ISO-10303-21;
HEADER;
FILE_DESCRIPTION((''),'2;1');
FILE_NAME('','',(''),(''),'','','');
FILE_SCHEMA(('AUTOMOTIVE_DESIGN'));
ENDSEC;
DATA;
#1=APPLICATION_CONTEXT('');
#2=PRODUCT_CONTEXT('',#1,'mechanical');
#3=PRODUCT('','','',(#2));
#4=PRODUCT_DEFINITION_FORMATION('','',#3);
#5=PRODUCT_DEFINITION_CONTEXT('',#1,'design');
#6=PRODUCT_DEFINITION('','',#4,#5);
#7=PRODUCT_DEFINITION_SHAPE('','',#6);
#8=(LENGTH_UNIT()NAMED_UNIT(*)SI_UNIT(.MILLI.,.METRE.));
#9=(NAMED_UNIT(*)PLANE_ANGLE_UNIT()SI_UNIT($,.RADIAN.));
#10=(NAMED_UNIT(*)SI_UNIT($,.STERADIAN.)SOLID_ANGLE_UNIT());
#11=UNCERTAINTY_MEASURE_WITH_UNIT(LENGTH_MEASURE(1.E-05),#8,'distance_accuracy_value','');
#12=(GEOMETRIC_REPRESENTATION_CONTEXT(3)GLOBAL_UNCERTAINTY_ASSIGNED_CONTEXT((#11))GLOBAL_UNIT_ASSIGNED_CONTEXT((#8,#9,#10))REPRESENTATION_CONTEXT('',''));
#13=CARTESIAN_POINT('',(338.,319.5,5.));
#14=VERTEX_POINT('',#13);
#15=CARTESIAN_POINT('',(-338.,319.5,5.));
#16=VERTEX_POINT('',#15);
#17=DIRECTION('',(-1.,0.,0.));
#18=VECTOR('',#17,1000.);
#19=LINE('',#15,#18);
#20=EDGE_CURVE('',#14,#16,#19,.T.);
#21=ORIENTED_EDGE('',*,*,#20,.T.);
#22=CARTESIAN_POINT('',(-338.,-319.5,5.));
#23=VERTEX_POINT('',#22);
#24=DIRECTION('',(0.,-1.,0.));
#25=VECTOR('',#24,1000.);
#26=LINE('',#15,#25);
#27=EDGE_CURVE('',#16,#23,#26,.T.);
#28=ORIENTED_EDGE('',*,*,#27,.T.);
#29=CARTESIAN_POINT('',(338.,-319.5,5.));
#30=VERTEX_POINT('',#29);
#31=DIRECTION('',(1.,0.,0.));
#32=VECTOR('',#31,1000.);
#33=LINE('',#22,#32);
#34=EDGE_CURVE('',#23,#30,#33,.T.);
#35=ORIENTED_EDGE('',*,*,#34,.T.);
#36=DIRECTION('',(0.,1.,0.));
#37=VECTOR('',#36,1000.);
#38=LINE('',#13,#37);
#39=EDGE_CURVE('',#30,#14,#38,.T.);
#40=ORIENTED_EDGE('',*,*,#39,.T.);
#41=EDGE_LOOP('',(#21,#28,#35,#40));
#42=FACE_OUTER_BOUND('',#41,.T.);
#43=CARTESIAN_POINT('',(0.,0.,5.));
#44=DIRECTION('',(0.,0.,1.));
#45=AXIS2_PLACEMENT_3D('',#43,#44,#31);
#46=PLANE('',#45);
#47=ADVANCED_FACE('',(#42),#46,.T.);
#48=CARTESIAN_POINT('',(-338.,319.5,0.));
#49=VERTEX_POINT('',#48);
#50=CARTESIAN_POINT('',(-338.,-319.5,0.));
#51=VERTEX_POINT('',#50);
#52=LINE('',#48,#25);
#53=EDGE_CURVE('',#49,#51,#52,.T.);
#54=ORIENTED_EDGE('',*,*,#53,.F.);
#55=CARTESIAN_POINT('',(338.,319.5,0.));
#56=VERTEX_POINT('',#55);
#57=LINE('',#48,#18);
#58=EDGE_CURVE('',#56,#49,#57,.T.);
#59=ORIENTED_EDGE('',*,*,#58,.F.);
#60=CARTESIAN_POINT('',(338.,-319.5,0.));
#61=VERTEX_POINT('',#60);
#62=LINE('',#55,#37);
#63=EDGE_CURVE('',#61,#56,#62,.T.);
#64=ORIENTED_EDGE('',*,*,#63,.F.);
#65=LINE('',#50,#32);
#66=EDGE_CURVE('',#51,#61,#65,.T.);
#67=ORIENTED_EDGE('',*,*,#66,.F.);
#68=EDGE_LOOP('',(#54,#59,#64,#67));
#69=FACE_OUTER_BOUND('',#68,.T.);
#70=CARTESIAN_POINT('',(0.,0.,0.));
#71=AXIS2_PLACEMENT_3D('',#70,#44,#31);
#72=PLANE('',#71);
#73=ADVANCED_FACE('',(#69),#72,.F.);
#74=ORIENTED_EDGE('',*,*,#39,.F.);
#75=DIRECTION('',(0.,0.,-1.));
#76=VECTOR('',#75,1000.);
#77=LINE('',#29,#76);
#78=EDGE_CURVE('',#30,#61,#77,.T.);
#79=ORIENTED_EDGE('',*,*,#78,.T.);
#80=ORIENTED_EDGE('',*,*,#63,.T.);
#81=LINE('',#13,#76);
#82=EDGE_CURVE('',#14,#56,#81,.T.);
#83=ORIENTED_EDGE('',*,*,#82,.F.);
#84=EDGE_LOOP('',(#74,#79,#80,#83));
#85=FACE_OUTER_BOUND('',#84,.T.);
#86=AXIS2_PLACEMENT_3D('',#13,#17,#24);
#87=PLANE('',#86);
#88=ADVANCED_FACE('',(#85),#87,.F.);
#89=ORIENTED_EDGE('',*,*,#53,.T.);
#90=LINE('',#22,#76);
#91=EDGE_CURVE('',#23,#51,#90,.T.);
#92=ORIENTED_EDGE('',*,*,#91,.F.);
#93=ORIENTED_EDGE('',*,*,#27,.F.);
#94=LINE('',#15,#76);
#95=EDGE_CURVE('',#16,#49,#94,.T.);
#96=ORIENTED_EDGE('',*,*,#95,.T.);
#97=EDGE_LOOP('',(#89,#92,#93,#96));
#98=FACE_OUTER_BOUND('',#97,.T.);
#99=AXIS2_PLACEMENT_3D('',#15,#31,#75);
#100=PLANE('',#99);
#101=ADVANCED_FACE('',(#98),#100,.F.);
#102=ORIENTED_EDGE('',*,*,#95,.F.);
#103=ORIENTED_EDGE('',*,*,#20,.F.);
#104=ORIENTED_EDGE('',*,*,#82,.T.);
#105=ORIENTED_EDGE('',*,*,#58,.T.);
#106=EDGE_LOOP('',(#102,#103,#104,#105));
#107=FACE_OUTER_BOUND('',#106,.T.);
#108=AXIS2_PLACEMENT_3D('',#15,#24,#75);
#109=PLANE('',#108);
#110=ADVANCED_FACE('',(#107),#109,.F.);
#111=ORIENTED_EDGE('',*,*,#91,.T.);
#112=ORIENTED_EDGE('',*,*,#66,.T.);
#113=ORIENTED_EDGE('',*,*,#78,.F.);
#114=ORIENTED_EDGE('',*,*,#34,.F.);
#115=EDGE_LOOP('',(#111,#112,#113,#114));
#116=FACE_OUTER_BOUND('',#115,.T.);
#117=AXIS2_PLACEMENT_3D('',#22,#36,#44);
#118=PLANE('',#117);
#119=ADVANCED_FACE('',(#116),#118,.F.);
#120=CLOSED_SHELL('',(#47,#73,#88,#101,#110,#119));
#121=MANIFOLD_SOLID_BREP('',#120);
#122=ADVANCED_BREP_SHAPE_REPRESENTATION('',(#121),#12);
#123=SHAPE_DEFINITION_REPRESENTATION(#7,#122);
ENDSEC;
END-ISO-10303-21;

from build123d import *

# Parameters (mm, degrees)
SKETCH_1_W      = 676
SKETCH_1_H      = 639
EXTRUDE_1_DEPTH = 5


with BuildPart() as part:
    # 草图1 → 凸台-拉伸1 (new body)
    with BuildSketch(Plane.XY):
        Rectangle(SKETCH_1_W, SKETCH_1_H)
    extrude(amount=EXTRUDE_1_DEPTH)


solid = part.part
